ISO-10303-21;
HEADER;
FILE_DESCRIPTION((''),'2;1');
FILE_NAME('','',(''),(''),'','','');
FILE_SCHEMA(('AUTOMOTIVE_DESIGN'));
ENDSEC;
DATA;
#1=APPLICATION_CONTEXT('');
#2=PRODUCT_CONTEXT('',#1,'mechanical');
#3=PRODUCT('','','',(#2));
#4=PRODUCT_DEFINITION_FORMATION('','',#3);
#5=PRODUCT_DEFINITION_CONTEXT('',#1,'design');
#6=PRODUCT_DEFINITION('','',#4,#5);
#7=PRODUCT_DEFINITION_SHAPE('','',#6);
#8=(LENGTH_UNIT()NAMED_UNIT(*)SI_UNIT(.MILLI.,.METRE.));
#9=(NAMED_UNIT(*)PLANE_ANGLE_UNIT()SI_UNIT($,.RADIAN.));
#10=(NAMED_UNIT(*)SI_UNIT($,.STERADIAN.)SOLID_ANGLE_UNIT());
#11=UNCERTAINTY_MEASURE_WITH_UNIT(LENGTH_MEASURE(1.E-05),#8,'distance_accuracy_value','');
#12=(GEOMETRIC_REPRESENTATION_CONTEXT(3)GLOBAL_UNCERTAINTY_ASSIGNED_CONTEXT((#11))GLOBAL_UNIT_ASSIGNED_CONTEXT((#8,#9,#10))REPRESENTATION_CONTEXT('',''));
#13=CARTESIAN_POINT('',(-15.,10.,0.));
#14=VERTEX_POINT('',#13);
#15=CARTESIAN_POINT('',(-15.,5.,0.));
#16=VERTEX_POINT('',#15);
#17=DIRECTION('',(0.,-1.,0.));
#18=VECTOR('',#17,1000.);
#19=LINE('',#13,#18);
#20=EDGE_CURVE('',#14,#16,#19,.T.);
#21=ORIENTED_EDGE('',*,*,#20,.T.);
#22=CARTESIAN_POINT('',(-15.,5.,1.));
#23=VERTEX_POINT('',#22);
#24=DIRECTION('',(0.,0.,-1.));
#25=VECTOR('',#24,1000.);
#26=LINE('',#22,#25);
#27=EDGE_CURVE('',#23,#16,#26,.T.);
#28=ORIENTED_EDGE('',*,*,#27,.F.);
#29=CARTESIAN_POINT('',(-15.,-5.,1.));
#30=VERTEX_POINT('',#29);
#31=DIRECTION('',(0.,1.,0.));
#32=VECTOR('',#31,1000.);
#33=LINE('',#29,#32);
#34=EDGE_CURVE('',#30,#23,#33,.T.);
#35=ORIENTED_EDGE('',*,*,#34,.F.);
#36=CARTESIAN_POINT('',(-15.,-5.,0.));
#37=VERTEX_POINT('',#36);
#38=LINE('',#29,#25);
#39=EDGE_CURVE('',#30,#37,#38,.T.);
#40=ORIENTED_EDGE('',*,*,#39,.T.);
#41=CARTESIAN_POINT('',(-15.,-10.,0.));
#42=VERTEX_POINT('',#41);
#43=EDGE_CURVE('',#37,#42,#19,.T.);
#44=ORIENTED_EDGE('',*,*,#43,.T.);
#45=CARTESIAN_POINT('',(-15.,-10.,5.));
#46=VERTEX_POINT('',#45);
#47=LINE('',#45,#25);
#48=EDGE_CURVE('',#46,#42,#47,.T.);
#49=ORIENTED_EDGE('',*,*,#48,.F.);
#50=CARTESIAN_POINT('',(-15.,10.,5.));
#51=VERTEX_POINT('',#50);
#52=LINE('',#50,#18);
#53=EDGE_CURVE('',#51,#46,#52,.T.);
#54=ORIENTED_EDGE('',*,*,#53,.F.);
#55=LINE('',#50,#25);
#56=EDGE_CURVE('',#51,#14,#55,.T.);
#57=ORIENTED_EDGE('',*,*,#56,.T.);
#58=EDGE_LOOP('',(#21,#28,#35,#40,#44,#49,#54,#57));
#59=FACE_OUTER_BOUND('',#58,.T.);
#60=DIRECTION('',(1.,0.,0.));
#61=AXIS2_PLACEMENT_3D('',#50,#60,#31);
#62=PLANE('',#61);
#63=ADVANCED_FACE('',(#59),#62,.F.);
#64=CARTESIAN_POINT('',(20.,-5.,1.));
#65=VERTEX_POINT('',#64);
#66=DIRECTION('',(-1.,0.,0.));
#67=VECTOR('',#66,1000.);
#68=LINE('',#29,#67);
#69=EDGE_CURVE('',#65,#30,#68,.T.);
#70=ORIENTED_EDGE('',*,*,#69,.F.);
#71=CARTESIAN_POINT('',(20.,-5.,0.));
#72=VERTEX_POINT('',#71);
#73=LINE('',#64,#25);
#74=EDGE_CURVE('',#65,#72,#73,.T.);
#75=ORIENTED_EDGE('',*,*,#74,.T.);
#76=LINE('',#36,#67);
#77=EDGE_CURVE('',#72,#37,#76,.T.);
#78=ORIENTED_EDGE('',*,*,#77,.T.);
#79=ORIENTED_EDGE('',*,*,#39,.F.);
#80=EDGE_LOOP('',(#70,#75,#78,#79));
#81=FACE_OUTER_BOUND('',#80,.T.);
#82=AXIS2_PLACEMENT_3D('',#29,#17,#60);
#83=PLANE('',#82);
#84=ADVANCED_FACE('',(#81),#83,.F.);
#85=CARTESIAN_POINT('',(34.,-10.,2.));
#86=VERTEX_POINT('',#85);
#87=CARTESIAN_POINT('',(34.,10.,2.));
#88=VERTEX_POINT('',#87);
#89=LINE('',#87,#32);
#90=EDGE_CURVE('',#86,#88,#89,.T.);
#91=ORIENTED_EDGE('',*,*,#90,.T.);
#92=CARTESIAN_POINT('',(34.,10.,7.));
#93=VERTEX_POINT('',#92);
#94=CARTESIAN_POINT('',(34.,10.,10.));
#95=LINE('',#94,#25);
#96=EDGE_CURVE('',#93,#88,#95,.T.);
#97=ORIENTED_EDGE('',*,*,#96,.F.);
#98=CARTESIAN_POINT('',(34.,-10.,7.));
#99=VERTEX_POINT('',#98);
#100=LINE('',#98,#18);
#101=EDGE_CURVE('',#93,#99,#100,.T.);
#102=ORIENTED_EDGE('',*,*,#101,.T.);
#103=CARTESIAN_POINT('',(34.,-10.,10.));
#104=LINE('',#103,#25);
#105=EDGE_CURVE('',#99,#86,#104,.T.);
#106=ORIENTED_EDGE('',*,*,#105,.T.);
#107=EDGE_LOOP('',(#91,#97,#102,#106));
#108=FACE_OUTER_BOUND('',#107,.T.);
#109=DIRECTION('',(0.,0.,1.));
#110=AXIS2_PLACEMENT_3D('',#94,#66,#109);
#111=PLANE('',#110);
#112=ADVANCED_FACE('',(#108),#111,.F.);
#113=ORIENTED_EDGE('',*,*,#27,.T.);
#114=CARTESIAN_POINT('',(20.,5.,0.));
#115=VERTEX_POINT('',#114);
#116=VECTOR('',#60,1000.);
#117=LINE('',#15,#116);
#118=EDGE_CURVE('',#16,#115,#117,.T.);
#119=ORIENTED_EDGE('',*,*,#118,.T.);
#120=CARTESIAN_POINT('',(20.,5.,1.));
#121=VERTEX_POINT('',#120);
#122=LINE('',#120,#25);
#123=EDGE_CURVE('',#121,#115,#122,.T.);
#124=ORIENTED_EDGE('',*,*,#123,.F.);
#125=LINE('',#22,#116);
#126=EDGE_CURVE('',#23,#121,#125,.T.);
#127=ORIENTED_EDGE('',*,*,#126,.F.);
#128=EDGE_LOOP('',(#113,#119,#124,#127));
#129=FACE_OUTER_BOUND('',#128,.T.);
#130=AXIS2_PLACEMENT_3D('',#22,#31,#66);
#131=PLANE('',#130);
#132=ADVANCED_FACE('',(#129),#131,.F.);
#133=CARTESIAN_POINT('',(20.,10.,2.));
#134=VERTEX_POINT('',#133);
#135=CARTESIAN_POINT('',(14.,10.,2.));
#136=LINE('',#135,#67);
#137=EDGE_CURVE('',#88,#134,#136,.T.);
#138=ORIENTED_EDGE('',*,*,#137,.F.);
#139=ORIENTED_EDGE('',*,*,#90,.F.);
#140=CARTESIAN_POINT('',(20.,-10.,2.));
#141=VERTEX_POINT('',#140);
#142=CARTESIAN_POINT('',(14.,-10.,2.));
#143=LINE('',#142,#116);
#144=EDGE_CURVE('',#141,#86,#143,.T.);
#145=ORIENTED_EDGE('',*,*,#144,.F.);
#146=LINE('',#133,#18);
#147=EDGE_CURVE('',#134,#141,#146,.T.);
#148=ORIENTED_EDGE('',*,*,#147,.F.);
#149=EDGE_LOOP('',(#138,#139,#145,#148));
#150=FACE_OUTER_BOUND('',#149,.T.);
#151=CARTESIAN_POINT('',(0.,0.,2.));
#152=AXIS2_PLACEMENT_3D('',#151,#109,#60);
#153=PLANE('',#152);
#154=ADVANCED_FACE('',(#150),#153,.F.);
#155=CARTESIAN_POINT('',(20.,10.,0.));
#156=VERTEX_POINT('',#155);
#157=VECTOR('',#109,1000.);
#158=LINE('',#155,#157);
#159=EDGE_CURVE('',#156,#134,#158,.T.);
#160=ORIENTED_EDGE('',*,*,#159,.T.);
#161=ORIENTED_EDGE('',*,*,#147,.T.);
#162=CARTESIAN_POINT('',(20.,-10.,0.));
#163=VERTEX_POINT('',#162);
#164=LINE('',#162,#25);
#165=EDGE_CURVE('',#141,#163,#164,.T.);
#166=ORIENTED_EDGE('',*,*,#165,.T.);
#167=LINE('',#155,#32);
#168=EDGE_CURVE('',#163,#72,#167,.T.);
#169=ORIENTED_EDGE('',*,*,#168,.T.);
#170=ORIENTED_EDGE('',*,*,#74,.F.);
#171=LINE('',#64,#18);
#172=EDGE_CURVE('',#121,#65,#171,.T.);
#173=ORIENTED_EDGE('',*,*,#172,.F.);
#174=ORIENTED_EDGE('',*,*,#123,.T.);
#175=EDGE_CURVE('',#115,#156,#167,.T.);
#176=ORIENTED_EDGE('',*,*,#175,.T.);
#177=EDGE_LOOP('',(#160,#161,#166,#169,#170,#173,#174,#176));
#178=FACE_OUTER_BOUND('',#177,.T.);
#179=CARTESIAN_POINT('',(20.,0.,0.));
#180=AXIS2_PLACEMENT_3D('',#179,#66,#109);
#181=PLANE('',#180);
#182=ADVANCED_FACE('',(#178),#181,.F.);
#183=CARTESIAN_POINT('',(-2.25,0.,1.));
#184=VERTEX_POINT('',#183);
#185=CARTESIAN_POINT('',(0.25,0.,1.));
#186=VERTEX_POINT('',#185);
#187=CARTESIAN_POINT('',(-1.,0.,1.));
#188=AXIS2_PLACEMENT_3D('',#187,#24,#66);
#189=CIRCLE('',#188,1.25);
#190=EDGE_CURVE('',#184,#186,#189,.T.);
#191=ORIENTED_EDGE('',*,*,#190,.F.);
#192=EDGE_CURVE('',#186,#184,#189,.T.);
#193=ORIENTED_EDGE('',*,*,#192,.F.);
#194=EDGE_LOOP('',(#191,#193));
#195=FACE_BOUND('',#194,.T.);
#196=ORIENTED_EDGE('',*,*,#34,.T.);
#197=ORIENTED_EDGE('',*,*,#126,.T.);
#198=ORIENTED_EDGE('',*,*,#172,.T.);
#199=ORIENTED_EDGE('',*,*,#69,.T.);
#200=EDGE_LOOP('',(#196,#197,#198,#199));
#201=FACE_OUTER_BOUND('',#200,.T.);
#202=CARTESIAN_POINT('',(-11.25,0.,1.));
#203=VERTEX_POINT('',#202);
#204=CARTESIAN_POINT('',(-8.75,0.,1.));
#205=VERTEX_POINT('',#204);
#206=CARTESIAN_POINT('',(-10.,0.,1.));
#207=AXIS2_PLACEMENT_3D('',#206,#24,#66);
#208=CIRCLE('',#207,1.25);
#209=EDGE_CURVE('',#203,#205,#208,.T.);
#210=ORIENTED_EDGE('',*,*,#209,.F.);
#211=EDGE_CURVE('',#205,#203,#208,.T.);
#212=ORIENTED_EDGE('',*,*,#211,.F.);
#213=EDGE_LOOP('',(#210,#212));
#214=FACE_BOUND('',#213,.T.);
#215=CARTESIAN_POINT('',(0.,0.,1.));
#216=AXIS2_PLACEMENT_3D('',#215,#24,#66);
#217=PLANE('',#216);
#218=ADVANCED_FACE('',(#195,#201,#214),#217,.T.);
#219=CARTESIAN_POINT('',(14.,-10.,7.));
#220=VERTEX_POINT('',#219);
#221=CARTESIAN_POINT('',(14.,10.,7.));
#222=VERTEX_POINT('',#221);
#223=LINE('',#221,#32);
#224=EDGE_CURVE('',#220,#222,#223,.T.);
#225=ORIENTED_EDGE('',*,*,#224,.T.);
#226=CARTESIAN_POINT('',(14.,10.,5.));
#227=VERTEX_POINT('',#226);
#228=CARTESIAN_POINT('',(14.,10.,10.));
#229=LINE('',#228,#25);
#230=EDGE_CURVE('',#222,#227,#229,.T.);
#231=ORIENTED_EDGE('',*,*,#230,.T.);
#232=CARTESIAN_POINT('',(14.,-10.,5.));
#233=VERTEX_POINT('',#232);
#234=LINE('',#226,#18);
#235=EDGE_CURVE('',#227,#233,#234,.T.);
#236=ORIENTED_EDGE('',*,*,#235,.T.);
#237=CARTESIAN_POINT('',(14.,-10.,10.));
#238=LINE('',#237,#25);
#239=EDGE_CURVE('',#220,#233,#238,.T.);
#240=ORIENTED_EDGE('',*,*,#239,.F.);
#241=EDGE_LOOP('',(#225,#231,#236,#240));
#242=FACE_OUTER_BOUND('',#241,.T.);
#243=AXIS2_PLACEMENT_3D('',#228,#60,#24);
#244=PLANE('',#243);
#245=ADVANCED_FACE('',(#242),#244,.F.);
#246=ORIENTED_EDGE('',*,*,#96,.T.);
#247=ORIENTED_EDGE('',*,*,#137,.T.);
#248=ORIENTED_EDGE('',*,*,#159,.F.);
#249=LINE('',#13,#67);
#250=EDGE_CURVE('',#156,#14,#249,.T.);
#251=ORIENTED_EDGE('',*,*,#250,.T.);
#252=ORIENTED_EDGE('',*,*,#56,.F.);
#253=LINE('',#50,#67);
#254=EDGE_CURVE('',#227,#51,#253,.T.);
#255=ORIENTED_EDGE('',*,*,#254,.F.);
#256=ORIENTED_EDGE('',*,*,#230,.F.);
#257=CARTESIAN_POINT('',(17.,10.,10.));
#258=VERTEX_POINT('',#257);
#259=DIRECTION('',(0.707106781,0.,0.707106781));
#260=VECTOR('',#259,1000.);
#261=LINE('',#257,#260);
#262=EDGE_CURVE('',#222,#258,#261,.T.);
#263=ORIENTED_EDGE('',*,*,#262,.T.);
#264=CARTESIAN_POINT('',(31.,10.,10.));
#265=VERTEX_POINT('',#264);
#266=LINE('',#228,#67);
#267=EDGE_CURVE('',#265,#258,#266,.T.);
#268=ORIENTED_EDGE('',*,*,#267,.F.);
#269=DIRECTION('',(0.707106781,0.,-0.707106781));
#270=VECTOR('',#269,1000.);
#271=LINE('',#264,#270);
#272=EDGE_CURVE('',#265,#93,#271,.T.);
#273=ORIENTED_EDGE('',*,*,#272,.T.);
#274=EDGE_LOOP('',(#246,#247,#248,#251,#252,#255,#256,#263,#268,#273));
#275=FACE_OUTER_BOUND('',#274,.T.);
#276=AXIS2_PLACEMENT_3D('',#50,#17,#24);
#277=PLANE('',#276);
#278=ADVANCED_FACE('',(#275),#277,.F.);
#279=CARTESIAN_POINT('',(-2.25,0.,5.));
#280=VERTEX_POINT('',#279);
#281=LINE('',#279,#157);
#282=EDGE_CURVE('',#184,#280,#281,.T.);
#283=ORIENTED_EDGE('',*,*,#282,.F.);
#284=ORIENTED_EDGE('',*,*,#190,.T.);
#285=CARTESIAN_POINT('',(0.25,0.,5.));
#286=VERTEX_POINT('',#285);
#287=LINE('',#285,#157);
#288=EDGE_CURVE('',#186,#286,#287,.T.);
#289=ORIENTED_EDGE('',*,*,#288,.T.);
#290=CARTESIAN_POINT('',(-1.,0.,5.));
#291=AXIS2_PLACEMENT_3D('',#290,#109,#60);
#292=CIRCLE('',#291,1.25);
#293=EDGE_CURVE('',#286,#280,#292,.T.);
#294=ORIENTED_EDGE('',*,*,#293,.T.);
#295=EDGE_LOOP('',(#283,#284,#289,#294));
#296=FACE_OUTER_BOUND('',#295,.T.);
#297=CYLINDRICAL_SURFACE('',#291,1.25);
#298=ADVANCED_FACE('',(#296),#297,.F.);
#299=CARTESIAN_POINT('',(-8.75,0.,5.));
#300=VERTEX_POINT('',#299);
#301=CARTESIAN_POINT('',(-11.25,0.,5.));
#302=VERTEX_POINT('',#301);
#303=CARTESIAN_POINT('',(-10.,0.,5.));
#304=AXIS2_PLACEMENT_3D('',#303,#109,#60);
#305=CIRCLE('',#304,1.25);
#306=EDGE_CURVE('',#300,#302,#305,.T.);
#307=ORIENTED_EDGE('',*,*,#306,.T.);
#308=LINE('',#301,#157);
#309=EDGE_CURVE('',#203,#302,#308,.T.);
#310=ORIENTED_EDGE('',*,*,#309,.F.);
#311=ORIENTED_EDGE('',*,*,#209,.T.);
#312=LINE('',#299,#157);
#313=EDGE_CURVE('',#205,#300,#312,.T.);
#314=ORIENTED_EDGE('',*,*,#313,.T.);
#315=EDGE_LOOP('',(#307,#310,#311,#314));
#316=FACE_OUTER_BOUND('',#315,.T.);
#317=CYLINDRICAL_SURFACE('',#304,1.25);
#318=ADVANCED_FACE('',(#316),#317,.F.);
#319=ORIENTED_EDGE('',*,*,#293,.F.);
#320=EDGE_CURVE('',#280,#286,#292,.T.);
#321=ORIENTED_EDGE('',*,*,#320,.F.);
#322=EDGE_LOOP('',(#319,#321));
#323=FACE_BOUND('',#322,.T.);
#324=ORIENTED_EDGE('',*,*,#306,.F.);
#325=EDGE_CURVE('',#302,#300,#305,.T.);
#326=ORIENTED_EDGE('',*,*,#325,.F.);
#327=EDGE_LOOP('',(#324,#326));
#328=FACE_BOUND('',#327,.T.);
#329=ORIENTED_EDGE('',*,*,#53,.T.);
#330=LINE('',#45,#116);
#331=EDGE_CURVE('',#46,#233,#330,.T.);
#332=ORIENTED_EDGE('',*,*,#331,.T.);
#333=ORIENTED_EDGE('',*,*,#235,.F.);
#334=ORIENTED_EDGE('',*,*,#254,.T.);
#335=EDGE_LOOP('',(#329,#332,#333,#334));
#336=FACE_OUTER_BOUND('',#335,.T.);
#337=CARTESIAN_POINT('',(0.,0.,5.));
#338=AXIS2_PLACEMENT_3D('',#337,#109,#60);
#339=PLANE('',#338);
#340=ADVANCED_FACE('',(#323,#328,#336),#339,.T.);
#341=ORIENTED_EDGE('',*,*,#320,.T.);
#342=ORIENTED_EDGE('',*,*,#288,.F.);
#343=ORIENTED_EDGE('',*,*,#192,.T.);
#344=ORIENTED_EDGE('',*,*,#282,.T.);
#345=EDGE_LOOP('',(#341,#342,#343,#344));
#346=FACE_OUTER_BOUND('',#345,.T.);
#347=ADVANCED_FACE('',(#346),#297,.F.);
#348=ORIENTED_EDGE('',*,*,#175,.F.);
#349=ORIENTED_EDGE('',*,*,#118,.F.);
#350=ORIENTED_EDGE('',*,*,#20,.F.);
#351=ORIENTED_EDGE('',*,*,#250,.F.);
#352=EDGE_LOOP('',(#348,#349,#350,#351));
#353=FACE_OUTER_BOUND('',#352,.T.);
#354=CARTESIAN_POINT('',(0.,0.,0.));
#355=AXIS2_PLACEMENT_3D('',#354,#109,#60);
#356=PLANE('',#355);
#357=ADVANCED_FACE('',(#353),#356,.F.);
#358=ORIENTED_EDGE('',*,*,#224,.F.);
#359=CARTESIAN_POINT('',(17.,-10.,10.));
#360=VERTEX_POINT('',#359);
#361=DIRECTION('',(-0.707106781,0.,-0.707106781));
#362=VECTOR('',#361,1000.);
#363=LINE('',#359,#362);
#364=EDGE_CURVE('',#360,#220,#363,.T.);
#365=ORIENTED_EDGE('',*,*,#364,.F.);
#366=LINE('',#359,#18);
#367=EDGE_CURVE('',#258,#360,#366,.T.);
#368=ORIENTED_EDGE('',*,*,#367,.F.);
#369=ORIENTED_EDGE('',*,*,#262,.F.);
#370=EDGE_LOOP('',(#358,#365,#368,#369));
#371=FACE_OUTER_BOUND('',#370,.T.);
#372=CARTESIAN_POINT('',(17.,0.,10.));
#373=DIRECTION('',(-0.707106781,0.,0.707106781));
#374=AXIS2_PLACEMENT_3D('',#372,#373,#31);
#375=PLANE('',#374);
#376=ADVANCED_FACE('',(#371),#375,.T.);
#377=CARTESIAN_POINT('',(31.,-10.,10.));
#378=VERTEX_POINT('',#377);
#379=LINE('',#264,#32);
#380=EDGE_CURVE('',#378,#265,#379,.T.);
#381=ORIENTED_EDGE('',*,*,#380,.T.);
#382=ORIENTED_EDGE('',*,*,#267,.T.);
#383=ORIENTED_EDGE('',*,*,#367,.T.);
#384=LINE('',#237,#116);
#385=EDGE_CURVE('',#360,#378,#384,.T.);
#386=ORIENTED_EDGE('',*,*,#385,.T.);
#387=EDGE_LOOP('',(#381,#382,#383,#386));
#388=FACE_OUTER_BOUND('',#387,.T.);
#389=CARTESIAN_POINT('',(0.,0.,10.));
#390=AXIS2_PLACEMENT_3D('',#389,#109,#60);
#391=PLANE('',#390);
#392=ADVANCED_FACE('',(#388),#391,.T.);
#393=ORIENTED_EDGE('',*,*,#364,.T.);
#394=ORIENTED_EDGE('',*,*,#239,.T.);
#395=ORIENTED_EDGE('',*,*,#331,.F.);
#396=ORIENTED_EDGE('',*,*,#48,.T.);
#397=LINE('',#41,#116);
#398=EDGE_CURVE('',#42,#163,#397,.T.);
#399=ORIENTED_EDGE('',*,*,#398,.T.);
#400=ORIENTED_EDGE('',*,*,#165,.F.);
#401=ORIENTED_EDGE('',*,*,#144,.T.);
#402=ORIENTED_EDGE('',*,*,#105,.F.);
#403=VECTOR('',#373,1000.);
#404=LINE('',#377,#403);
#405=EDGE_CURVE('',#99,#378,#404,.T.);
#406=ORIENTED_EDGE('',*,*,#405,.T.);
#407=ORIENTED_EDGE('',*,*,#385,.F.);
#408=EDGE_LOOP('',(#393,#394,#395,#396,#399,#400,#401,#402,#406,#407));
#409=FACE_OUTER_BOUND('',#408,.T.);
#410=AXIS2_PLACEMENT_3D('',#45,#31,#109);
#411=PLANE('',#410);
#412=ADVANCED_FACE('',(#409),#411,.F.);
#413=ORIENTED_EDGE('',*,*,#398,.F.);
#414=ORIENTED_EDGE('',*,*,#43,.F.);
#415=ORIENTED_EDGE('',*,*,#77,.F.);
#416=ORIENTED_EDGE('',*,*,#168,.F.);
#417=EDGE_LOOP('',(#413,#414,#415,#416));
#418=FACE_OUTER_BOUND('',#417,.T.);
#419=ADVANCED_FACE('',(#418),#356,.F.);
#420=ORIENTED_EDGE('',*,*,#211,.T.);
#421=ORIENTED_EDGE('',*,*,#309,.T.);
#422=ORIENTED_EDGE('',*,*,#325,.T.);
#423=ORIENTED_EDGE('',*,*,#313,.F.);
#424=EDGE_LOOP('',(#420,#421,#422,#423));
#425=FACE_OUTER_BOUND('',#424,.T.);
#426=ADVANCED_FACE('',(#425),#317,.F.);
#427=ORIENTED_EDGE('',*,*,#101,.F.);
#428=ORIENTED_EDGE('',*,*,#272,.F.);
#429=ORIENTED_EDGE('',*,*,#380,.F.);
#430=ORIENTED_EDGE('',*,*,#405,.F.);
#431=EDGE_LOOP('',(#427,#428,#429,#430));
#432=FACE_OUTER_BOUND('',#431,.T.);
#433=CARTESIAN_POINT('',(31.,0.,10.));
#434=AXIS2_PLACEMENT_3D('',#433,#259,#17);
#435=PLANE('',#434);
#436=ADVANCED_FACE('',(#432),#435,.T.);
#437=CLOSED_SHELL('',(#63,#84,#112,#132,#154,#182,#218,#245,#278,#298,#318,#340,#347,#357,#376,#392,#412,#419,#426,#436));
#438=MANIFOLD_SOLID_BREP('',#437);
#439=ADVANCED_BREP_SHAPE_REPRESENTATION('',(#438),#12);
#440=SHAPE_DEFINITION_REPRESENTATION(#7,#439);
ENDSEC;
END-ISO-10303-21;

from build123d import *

# Parameters (mm, degrees)
SKETCH_1_W          = 30
SKETCH_1_H          = 20
EXTRUDE_1_DEPTH     = 5
SKETCH_2_W          = 5
SKETCH_2_H          = 20
EXTRUDE_2_DEPTH     = 5
SKETCH_4_W          = 35
SKETCH_4_H          = 10
CUT_EXTRUDE_1_DEPTH = 1
SKETCH_5_W          = 20
SKETCH_5_H          = 20
EXTRUDE_4_DEPTH     = 5
CHAMFER_1_SIZE      = 3
CHAMFER_2_SIZE      = 3
M3X0_5_1_D          = 2.5
MOVE_FACE_1_BY      = 3


with BuildPart() as part:
    # 草图1 → 凸台-拉伸1 (new body)
    with BuildSketch(Plane.XY):
        Rectangle(SKETCH_1_W, SKETCH_1_H)
    extrude(amount=EXTRUDE_1_DEPTH)

    # 草图2 → 凸台-拉伸2 (add)
    with BuildSketch(Plane(origin=(15, 0, 0), x_dir=(0, 0, -1), z_dir=(1, 0, 0))):
        with Locations((-2.5, 0)):
            Rectangle(SKETCH_2_W, SKETCH_2_H)
    extrude(amount=EXTRUDE_2_DEPTH)

    # 草图4 → 切除-拉伸1 (cut)
    with BuildSketch(Plane(origin=(0, 0, 0), x_dir=(-1, 0, 0), z_dir=(0, 0, -1))):
        with Locations((-2.5, 0)):
            Rectangle(SKETCH_4_W, SKETCH_4_H)
    extrude(amount=-CUT_EXTRUDE_1_DEPTH, mode=Mode.SUBTRACT)

    # 草图5 → 凸台-拉伸4 (add)
    with BuildSketch(Plane.XY.offset(5)):
        with Locations((24, 0)):
            Rectangle(SKETCH_5_W, SKETCH_5_H)
    extrude(amount=EXTRUDE_4_DEPTH)

    # 倒角1
    chamfer_1_edges = [part.edges().sort_by_distance(p)[0] for p in [
        (14, 0, 10),
    ]]
    chamfer(chamfer_1_edges, length=CHAMFER_1_SIZE)

    # 倒角2
    chamfer_2_edges = [part.edges().sort_by_distance(p)[0] for p in [
        (34, 0, 10),
    ]]
    chamfer(chamfer_2_edges, length=CHAMFER_2_SIZE)

    # M3x0.5 螺纹孔1 (through all)
    with Locations(Plane.XY.offset(5)):
        with Locations((-10, 0), (-1, 0)):
            Hole(M3X0_5_1_D / 2)

    # Move Face 1: a face moved outward by 3.0
    extrude(part.faces().sort_by_distance((27, 0, 5))[0], amount=MOVE_FACE_1_BY, dir=(0, 0, -1))


solid = part.part
